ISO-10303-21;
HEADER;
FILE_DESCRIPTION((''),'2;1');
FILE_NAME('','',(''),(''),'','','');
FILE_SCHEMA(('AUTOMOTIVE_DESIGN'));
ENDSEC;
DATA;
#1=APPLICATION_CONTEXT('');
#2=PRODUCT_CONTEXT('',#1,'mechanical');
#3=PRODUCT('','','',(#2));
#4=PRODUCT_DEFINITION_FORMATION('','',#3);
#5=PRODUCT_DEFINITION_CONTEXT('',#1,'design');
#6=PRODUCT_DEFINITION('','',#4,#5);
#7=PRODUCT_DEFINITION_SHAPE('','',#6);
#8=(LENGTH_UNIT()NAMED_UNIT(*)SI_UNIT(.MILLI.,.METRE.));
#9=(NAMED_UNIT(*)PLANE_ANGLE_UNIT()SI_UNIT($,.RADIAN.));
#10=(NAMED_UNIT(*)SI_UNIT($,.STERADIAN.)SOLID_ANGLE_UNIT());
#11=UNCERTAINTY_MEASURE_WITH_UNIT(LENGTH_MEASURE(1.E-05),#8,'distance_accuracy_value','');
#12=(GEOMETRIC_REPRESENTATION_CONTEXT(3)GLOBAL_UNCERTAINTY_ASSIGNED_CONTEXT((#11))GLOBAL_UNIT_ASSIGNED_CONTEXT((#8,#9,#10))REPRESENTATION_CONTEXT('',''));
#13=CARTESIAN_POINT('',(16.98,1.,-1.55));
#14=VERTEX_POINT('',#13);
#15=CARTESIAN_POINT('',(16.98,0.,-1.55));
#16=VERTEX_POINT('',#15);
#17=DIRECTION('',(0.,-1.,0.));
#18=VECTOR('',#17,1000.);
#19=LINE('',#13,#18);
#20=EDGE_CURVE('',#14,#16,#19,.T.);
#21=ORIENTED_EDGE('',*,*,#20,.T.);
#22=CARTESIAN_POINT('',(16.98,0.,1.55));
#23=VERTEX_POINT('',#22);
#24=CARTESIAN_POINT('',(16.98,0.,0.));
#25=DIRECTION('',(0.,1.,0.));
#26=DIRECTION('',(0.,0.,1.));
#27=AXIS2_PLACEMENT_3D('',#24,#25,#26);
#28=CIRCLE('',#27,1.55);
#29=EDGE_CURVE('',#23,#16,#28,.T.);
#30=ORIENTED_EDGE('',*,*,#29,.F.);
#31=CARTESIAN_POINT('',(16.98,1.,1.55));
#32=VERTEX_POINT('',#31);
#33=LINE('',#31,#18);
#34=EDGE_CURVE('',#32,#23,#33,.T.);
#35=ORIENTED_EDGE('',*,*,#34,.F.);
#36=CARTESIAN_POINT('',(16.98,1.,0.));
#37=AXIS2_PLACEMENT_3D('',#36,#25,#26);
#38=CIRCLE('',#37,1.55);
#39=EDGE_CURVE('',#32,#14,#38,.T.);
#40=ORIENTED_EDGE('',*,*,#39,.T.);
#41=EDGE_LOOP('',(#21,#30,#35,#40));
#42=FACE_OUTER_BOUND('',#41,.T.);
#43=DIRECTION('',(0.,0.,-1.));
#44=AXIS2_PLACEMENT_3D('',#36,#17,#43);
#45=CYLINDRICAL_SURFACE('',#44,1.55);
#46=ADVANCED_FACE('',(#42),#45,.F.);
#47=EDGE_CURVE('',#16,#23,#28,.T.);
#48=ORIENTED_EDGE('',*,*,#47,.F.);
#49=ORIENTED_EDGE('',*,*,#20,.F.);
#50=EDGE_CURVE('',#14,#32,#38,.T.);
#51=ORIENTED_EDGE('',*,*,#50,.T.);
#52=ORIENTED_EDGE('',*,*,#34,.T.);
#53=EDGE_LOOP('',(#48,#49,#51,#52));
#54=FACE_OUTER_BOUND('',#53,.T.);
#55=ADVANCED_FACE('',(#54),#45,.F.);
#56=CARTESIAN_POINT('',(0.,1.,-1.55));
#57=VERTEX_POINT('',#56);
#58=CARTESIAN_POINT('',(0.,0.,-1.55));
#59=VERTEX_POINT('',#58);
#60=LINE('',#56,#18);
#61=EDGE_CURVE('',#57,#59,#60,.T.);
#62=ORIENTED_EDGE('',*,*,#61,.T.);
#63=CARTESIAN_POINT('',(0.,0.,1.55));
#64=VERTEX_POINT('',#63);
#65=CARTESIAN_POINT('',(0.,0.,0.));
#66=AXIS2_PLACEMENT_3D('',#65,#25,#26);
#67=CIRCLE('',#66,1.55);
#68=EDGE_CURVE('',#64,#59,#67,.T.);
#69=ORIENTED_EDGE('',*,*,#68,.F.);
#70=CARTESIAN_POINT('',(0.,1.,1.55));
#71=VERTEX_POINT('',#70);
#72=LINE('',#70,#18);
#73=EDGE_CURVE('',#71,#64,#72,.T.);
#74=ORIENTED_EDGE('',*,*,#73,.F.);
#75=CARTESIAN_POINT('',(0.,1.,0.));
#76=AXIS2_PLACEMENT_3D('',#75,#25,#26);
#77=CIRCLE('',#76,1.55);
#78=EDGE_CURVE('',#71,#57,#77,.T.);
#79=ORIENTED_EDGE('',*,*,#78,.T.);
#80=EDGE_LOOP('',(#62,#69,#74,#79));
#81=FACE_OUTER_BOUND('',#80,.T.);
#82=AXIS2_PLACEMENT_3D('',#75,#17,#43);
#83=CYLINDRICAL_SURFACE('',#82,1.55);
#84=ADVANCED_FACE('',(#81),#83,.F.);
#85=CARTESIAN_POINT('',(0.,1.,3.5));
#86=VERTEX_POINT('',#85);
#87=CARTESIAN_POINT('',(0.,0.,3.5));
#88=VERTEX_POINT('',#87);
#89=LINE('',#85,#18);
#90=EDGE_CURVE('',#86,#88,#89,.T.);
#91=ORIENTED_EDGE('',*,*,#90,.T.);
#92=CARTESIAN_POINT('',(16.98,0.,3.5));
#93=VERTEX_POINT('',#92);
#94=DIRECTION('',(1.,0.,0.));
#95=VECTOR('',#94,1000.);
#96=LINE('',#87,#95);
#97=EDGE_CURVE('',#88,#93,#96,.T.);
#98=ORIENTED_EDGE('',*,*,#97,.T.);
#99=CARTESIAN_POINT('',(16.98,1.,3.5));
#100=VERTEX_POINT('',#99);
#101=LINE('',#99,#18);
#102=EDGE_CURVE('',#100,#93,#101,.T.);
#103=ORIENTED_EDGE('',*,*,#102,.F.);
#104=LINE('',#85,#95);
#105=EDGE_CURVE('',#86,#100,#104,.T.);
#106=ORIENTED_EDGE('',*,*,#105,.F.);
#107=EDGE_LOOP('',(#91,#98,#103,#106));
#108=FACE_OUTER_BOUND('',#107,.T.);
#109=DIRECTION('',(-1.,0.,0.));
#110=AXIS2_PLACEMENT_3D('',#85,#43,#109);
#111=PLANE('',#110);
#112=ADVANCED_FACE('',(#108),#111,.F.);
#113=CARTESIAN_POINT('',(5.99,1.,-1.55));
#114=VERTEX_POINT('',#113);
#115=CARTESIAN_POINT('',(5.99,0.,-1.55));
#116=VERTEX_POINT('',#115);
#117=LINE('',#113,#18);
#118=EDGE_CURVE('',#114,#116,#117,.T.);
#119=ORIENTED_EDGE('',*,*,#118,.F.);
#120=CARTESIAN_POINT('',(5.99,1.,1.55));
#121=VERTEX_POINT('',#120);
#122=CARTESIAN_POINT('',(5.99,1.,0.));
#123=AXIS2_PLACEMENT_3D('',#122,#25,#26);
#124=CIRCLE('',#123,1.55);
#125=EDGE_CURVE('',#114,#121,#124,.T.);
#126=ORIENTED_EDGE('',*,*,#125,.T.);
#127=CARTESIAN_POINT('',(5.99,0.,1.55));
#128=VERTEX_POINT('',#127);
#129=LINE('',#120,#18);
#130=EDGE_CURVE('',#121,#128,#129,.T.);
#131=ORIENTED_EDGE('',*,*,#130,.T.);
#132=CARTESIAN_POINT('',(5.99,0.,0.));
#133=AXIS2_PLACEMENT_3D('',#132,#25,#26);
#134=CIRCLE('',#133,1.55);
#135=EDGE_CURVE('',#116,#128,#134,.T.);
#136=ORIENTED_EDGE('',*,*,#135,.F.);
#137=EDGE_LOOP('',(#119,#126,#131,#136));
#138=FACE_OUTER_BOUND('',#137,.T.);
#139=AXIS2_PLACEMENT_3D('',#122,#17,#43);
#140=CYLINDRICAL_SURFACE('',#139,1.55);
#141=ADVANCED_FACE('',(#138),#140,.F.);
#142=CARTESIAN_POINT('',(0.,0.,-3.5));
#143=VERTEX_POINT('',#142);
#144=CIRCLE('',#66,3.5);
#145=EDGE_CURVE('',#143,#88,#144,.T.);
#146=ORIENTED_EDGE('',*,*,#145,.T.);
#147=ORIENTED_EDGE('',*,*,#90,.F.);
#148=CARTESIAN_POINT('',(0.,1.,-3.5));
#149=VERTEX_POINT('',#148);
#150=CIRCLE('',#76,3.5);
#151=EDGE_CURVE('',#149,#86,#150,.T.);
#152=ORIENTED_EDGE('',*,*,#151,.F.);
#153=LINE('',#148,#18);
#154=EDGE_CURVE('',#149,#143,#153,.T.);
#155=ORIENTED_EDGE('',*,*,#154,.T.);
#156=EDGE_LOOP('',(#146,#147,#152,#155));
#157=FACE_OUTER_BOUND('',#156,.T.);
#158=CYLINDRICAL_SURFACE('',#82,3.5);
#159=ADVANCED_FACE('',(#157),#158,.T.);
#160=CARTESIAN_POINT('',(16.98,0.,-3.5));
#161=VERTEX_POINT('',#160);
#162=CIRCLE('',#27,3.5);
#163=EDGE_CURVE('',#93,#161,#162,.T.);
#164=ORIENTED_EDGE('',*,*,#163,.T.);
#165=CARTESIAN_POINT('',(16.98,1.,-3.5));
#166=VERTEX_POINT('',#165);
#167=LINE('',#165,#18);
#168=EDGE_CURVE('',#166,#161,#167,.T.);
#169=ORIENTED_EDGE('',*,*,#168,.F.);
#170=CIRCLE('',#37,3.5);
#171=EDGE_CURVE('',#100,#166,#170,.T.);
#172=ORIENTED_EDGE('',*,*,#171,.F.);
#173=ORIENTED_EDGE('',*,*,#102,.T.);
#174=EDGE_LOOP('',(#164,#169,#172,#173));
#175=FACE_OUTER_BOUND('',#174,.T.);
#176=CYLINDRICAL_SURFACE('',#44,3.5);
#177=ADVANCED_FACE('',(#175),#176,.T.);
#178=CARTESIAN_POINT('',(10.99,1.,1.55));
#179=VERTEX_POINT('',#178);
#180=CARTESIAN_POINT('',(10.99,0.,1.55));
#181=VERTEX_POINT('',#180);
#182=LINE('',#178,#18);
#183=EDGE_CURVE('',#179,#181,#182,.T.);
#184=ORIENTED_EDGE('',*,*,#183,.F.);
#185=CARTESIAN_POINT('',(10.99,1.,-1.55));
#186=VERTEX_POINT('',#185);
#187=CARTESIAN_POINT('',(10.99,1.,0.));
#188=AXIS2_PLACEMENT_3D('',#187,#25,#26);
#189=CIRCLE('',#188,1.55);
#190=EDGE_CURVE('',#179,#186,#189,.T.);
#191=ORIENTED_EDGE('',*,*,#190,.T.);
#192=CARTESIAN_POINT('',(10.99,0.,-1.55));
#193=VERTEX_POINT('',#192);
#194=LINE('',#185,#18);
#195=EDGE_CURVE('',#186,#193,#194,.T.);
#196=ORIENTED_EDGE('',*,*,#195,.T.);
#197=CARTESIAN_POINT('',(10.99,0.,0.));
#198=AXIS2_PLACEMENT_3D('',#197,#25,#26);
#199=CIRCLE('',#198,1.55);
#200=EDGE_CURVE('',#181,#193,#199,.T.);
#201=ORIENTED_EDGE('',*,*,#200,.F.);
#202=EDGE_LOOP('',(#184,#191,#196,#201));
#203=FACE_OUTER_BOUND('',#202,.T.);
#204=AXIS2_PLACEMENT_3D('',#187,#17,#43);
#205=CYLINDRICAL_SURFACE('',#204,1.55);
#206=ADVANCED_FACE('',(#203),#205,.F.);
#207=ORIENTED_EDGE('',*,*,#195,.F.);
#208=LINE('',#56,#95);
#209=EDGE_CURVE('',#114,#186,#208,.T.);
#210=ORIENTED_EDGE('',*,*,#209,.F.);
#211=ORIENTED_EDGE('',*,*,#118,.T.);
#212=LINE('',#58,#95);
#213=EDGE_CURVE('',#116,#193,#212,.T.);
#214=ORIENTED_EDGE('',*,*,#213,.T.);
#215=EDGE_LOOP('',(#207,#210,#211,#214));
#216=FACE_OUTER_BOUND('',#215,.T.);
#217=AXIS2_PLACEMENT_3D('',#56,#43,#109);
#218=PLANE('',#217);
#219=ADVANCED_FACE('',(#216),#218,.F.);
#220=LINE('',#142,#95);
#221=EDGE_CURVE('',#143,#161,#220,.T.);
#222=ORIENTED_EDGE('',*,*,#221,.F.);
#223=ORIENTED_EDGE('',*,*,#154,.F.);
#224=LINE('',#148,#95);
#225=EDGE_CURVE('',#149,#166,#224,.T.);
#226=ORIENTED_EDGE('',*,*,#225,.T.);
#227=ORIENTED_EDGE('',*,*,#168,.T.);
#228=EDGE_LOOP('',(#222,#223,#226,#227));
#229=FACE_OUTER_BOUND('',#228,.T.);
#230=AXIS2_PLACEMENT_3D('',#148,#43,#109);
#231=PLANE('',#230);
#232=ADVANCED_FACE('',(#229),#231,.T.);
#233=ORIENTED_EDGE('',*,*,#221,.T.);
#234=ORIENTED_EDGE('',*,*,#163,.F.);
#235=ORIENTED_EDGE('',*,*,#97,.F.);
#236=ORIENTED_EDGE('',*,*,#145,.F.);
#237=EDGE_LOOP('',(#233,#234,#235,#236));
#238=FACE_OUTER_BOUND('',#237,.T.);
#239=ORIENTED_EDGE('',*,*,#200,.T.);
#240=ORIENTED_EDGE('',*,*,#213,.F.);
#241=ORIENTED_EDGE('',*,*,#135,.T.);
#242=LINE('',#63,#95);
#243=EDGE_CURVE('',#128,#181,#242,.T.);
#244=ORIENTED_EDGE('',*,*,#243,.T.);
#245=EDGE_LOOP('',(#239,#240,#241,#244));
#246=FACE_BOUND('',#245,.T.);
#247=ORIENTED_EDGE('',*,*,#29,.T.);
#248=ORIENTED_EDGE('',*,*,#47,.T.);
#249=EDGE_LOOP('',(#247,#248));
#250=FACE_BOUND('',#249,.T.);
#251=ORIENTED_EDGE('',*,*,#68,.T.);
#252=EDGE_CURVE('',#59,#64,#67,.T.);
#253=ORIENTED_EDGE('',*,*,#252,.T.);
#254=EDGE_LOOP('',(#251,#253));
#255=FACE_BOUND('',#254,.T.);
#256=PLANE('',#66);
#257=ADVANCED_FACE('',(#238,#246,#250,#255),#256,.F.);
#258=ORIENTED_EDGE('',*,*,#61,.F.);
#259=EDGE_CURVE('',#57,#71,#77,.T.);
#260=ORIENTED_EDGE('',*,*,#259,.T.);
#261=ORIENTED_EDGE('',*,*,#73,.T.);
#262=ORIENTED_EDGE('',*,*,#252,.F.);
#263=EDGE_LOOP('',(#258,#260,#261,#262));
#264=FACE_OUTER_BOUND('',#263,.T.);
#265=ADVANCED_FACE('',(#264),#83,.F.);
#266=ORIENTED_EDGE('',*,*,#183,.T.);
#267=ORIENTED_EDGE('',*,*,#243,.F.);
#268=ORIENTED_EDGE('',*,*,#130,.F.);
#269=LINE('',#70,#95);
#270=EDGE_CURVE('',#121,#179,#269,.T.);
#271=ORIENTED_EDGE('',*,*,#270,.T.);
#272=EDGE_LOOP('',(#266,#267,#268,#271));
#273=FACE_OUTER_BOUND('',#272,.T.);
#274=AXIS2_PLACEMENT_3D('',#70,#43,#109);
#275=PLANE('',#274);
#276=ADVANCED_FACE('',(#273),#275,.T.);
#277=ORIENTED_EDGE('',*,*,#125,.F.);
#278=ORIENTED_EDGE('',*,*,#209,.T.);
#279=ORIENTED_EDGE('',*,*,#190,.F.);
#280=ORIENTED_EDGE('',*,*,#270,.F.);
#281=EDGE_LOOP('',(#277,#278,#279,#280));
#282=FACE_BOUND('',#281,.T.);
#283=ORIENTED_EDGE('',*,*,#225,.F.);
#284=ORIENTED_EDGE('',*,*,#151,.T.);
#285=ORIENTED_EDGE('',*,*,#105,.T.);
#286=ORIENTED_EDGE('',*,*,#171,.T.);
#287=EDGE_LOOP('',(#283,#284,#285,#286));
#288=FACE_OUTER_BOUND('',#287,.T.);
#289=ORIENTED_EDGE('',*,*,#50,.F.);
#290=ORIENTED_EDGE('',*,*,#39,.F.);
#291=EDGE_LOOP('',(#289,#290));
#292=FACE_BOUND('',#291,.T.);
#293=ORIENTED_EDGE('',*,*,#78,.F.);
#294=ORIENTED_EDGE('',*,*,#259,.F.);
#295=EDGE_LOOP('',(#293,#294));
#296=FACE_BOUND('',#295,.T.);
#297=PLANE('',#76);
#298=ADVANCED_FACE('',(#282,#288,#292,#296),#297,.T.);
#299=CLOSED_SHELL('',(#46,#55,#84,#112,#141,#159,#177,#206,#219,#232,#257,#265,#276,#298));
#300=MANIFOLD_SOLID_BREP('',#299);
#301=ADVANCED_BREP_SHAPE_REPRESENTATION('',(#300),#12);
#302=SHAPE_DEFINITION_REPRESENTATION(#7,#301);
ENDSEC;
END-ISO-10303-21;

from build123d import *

# Parameters (mm, degrees)
SKETCH_1_R      = 1.55
EXTRUDE_1_DEPTH = 1


with BuildPart() as part:
    # 草图1 → 凸台-拉伸1 (new body)
    with BuildSketch(Plane(origin=(0, 0, 0), x_dir=(1, 0, 0), z_dir=(0, 1, 0))):
        with BuildLine():
            ThreePointArc((0, 3.5), (-3.5, 0), (0, -3.5))
            Line((0, -3.5), (16.98, -3.5))
            ThreePointArc((16.98, -3.5), (20.48, 0), (16.98, 3.5))
            Line((16.98, 3.5), (0, 3.5))
        make_face()
        with Locations(Location((0, 0, 0), (0, 0, 270))):
            Circle(SKETCH_1_R, mode=Mode.SUBTRACT)
        with BuildLine():
            ThreePointArc((10.99, 1.55), (12.54, 0), (10.99, -1.55))
            Line((10.99, -1.55), (5.99, -1.55))
            ThreePointArc((5.99, -1.55), (4.44, 0), (5.99, 1.55))
            Line((5.99, 1.55), (10.99, 1.55))
        make_face(mode=Mode.SUBTRACT)
        with Locations(Location((16.98, 0, 0), (0, 0, 270))):
            Circle(SKETCH_1_R, mode=Mode.SUBTRACT)
    extrude(amount=EXTRUDE_1_DEPTH)


solid = part.part
